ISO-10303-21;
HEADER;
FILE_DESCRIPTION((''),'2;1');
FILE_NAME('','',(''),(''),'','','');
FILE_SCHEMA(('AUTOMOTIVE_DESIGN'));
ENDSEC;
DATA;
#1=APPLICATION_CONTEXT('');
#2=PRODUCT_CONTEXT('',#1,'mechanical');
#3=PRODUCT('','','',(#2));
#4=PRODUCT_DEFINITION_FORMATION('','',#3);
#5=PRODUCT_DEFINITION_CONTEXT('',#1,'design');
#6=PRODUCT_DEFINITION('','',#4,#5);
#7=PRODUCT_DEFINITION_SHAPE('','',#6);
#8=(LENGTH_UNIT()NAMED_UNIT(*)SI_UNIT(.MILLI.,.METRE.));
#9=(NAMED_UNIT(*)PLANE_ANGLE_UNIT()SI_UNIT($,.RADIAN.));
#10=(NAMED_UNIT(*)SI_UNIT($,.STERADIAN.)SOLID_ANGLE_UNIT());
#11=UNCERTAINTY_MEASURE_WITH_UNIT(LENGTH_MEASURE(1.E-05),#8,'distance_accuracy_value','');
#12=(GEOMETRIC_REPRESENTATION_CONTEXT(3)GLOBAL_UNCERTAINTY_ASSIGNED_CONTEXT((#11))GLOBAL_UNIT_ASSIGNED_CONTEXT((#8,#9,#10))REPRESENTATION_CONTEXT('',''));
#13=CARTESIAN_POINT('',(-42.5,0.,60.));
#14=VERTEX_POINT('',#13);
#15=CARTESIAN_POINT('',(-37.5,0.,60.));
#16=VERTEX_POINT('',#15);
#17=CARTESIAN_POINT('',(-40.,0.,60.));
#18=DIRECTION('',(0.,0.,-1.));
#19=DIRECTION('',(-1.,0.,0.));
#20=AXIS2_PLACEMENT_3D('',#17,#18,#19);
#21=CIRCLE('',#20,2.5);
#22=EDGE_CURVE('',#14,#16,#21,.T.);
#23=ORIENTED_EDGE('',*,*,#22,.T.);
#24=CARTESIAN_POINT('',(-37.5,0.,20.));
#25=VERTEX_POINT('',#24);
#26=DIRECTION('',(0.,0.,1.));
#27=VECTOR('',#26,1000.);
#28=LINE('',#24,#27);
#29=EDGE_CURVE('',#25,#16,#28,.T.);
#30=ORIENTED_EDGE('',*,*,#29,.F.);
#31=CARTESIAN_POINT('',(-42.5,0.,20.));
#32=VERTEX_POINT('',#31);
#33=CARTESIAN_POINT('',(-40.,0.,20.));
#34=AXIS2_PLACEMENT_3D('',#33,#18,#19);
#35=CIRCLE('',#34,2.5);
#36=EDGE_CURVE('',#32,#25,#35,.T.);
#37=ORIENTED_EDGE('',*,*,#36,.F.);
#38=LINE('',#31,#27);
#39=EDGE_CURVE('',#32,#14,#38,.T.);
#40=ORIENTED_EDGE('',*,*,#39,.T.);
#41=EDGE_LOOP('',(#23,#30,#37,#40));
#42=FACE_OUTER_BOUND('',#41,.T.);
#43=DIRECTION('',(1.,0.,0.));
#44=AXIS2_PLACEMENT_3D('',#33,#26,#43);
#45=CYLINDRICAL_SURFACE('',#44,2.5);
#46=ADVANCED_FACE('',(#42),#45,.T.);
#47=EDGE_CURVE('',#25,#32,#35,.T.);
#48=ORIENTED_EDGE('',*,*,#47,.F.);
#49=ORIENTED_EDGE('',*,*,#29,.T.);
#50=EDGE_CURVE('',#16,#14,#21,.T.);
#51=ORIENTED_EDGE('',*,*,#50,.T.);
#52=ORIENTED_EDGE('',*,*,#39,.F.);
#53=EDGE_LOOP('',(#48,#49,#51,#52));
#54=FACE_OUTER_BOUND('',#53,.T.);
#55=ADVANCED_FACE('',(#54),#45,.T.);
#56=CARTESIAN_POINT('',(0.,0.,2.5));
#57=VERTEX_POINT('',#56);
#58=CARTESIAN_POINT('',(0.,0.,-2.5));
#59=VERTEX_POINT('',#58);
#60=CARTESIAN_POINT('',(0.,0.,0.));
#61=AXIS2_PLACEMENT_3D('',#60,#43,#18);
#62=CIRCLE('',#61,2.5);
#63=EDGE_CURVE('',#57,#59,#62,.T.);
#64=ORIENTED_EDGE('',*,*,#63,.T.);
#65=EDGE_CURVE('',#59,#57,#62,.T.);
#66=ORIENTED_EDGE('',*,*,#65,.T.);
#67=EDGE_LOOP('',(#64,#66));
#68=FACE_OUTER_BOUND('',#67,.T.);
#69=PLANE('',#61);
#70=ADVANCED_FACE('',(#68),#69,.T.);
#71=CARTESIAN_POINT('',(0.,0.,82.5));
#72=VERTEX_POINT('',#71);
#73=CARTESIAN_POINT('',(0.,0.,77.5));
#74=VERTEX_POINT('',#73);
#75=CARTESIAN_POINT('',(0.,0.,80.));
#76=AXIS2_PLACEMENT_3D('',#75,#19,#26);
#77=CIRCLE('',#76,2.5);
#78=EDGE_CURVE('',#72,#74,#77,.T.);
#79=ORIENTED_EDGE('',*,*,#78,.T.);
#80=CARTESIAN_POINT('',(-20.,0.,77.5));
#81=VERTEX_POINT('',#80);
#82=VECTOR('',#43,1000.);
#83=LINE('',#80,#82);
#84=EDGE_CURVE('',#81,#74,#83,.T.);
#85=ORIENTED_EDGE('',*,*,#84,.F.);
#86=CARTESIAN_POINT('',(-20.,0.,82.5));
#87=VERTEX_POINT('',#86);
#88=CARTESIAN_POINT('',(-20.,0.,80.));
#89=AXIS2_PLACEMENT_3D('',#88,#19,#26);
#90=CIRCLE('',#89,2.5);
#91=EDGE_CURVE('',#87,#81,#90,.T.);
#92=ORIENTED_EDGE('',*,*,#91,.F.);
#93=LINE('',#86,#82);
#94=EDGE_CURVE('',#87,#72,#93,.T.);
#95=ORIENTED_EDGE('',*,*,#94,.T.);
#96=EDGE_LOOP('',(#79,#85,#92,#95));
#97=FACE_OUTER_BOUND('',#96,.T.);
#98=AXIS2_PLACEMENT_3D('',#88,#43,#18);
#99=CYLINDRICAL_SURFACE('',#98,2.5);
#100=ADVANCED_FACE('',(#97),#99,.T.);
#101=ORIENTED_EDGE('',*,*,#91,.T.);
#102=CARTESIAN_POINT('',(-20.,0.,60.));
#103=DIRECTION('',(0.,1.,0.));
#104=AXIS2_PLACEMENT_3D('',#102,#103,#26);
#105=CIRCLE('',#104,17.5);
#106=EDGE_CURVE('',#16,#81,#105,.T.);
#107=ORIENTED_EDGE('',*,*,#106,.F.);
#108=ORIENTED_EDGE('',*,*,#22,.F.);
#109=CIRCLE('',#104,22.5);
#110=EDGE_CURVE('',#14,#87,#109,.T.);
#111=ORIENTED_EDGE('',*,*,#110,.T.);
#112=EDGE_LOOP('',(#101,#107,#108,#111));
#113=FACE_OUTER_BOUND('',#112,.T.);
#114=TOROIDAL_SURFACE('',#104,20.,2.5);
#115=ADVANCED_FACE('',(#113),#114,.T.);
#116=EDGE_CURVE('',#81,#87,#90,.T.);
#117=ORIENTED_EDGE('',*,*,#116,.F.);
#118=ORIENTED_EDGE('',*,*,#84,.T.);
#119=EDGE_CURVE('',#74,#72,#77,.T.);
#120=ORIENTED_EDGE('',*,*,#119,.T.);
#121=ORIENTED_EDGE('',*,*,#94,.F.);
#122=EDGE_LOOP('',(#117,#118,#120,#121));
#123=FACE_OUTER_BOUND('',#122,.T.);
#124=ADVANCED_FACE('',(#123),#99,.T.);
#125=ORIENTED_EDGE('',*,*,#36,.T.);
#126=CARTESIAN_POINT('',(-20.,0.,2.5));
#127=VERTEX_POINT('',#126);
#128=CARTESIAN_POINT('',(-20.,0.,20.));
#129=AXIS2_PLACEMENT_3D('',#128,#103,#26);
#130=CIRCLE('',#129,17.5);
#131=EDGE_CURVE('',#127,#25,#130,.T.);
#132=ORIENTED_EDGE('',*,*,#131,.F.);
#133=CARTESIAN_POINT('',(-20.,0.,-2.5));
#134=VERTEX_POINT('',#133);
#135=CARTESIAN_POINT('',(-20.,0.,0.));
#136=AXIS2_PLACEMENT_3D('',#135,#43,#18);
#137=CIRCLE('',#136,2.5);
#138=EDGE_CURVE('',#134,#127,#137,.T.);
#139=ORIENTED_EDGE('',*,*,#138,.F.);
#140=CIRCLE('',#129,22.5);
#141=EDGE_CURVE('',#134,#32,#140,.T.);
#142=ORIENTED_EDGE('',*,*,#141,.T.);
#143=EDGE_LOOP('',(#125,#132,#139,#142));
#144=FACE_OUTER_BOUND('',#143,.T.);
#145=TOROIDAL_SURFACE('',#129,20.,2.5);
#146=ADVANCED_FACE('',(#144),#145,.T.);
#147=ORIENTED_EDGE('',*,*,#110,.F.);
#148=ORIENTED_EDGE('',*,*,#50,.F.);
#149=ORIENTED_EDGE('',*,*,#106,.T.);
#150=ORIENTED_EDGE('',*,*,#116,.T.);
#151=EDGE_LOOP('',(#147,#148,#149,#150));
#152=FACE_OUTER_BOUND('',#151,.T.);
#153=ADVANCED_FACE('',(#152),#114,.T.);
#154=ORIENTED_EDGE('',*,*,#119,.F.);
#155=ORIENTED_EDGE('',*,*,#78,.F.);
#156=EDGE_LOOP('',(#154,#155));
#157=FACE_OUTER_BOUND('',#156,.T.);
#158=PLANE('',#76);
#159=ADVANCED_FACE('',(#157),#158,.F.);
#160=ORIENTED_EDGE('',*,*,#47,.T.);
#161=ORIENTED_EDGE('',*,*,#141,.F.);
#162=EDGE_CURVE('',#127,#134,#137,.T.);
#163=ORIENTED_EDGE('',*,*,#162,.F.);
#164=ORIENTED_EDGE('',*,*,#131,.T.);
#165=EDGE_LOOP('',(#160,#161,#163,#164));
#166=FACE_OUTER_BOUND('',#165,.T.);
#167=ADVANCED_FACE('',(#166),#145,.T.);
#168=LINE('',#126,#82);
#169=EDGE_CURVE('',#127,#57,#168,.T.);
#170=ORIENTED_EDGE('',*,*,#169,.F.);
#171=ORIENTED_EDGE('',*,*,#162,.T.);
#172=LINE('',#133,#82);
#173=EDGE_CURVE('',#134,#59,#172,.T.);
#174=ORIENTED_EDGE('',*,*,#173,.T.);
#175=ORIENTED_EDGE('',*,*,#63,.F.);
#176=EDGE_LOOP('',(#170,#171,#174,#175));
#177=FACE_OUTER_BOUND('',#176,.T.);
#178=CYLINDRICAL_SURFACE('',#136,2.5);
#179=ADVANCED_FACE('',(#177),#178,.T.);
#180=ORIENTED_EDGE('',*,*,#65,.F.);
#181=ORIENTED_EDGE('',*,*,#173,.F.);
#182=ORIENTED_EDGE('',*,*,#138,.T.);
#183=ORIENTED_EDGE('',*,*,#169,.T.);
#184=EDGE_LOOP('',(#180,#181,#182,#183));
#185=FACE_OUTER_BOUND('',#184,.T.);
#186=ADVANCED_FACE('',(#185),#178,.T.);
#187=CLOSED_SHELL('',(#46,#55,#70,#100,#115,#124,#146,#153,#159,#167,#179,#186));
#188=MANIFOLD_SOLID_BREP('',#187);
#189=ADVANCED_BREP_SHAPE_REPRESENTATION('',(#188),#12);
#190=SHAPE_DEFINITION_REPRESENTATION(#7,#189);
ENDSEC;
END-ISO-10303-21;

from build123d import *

# Parameters (mm, degrees)
SKETCH2_R = 2.5


with BuildPart() as part:
    # Sweep1: sweep along a path in Sketch1
    with BuildLine(Plane(origin=(0, 0, 0), x_dir=(1, 0, 0), z_dir=(0, 1, 0))) as sweep1_path:
        Line((0, 0), (-20, 0))
        ThreePointArc((-20, 0), (-34.142135624, -5.857864376), (-40, -20))
        Line((-40, -20), (-40, -60))
        ThreePointArc((-40, -60), (-34.142135624, -74.142135624), (-20, -80))
        Line((-20, -80), (0, -80))
    # Sketch2 → Sweep1 (sweep)
    with BuildSketch(Plane(origin=(0, 0, 0), x_dir=(0, 0, -1), z_dir=(1, 0, 0))):
        Circle(SKETCH2_R)
    sweep(path=sweep1_path.line)


solid = part.part
